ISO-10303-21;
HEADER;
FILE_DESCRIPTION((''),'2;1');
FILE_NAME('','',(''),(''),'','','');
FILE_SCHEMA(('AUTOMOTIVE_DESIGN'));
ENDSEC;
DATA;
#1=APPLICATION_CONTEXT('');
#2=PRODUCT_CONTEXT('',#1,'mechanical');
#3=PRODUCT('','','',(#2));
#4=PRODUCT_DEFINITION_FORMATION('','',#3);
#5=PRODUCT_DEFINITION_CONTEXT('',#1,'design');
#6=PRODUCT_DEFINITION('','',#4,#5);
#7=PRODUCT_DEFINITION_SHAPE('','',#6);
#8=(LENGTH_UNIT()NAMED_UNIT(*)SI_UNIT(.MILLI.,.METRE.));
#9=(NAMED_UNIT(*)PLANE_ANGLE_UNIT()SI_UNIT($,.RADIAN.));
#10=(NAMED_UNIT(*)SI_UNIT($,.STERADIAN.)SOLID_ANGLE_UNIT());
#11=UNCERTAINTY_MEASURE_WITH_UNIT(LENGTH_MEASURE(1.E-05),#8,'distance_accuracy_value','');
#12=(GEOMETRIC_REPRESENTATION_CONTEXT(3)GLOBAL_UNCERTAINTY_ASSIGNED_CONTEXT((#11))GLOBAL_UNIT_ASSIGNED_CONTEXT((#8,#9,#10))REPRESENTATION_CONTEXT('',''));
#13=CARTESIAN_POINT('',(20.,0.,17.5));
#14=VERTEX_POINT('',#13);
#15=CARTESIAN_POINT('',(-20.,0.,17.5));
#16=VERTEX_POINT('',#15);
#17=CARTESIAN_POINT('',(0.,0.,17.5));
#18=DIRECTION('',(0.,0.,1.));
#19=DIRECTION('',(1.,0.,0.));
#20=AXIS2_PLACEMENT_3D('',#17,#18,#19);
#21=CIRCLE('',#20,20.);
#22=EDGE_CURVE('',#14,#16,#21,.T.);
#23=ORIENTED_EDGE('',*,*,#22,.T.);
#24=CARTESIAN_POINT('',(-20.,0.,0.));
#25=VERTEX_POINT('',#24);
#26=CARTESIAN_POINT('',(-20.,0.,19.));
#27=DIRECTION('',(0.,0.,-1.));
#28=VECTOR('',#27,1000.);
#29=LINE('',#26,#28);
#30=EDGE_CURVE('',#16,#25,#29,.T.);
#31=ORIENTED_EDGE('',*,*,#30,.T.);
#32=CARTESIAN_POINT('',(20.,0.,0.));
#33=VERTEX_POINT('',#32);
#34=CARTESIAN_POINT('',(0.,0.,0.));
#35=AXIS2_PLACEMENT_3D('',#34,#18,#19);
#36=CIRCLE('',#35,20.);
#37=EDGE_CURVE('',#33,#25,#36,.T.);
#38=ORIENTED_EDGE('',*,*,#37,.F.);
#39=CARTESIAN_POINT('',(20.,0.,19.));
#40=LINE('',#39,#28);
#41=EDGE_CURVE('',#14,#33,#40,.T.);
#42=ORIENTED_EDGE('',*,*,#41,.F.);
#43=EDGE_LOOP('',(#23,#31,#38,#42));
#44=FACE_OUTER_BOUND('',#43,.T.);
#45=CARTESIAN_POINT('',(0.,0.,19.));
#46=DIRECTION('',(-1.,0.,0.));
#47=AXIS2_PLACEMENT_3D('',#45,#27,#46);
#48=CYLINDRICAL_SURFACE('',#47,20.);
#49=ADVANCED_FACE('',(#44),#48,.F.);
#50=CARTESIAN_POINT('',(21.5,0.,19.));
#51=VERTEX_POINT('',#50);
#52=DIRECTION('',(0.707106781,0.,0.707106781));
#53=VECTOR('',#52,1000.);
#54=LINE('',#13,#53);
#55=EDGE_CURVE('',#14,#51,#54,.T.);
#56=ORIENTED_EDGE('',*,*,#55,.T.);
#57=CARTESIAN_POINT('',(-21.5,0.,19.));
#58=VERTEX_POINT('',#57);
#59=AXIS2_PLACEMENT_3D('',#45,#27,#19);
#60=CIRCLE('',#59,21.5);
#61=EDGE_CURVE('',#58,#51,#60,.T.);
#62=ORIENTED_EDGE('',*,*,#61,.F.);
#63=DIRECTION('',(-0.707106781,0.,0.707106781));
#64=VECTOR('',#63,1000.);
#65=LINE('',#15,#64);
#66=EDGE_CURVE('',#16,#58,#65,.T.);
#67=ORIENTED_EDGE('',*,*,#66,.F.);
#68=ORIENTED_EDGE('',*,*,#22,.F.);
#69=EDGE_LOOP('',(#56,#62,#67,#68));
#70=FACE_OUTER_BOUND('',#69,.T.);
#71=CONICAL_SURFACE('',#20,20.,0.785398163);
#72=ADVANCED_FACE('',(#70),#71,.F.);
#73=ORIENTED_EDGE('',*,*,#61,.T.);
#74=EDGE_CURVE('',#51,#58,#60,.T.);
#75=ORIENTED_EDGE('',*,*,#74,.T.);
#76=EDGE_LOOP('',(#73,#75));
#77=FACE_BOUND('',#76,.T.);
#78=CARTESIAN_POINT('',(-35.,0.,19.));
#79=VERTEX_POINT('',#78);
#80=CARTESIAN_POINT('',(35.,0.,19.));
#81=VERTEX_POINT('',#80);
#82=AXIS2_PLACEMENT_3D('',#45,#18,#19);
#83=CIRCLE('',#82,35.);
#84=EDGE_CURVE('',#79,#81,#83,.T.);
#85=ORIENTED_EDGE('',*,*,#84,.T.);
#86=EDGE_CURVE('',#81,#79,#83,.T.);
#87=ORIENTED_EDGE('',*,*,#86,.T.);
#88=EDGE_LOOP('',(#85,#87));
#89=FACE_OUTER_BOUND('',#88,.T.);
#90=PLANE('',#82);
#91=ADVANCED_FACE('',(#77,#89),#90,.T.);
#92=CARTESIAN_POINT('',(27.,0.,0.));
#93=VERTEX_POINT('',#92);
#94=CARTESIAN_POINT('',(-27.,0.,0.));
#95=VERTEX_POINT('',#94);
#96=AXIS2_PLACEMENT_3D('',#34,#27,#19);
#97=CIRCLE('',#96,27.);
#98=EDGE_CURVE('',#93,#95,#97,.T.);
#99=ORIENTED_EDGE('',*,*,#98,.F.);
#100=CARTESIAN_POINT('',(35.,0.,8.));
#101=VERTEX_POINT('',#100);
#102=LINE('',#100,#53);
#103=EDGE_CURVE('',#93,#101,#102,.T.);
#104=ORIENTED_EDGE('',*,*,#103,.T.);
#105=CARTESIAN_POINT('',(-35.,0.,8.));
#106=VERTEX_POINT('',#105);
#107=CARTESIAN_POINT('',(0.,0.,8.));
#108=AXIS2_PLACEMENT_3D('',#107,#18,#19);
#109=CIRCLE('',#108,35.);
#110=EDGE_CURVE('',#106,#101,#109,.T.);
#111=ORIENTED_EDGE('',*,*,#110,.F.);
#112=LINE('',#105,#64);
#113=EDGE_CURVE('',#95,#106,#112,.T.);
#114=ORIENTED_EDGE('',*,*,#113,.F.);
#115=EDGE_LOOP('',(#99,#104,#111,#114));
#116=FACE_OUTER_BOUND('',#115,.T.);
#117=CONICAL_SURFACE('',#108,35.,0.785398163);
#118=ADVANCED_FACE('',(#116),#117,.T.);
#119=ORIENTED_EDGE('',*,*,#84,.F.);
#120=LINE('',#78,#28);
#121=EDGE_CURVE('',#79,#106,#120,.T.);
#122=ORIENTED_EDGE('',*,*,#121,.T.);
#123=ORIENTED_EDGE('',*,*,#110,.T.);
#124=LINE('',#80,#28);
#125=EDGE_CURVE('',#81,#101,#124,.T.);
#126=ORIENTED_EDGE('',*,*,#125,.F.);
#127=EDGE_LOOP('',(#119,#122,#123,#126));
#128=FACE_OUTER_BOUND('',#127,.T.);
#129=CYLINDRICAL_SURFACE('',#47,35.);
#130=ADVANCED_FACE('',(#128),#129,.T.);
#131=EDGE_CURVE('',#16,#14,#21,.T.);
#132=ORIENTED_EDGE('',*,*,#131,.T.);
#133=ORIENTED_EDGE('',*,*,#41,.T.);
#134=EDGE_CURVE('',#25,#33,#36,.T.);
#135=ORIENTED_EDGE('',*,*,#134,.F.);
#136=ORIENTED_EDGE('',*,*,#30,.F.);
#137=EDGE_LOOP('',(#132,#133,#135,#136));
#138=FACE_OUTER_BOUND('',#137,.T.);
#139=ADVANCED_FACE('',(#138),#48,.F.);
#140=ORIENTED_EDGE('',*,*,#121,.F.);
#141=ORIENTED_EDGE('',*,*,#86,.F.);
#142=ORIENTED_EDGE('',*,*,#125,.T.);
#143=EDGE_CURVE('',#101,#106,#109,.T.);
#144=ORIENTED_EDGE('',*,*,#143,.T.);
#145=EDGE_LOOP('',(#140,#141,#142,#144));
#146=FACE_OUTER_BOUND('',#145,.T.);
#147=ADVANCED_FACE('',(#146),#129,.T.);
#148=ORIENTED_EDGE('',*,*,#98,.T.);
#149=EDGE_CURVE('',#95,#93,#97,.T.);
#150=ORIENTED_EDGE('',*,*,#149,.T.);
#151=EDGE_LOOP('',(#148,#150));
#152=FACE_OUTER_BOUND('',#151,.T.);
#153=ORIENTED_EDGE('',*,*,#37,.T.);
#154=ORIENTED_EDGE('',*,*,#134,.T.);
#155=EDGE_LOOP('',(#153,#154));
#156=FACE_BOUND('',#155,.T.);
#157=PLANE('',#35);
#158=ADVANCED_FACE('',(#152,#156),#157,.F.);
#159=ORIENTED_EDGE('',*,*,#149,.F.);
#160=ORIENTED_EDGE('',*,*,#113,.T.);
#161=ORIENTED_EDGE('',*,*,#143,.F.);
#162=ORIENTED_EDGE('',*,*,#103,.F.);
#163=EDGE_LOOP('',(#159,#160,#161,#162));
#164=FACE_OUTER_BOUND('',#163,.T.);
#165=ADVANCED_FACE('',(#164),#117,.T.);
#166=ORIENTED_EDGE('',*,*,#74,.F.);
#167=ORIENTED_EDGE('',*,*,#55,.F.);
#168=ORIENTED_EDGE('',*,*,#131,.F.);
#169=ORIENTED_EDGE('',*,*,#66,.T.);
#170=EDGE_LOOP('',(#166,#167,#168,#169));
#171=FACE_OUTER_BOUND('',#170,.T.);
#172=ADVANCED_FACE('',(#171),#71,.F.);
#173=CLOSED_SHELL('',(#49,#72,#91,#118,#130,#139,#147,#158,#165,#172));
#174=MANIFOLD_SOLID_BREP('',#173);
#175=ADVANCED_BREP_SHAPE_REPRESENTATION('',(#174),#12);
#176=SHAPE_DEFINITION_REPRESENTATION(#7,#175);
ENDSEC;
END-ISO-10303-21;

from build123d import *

# Parameters (mm, degrees)
SKETCH_1_R      = 35
SKETCH_1_R_2    = 20
EXTRUDE_1_DEPTH = 19
CHAMFER_1_SIZE  = 8
CHAMFER_2_SIZE  = 1.5


with BuildPart() as part:
    # 草图1 → 凸台-拉伸1 (new body)
    with BuildSketch(Plane.XY):
        Circle(SKETCH_1_R)
        Circle(SKETCH_1_R_2, mode=Mode.SUBTRACT)
    extrude(amount=EXTRUDE_1_DEPTH)

    # 倒角1
    chamfer_1_edges = [part.edges().sort_by_distance(p)[0] for p in [
        (-35, 0, 0),
    ]]
    chamfer(chamfer_1_edges, length=CHAMFER_1_SIZE)

    # 倒角2
    chamfer_2_edges = [part.edges().sort_by_distance(p)[0] for p in [
        (-20, 0, 19),
    ]]
    chamfer(chamfer_2_edges, length=CHAMFER_2_SIZE)


solid = part.part
